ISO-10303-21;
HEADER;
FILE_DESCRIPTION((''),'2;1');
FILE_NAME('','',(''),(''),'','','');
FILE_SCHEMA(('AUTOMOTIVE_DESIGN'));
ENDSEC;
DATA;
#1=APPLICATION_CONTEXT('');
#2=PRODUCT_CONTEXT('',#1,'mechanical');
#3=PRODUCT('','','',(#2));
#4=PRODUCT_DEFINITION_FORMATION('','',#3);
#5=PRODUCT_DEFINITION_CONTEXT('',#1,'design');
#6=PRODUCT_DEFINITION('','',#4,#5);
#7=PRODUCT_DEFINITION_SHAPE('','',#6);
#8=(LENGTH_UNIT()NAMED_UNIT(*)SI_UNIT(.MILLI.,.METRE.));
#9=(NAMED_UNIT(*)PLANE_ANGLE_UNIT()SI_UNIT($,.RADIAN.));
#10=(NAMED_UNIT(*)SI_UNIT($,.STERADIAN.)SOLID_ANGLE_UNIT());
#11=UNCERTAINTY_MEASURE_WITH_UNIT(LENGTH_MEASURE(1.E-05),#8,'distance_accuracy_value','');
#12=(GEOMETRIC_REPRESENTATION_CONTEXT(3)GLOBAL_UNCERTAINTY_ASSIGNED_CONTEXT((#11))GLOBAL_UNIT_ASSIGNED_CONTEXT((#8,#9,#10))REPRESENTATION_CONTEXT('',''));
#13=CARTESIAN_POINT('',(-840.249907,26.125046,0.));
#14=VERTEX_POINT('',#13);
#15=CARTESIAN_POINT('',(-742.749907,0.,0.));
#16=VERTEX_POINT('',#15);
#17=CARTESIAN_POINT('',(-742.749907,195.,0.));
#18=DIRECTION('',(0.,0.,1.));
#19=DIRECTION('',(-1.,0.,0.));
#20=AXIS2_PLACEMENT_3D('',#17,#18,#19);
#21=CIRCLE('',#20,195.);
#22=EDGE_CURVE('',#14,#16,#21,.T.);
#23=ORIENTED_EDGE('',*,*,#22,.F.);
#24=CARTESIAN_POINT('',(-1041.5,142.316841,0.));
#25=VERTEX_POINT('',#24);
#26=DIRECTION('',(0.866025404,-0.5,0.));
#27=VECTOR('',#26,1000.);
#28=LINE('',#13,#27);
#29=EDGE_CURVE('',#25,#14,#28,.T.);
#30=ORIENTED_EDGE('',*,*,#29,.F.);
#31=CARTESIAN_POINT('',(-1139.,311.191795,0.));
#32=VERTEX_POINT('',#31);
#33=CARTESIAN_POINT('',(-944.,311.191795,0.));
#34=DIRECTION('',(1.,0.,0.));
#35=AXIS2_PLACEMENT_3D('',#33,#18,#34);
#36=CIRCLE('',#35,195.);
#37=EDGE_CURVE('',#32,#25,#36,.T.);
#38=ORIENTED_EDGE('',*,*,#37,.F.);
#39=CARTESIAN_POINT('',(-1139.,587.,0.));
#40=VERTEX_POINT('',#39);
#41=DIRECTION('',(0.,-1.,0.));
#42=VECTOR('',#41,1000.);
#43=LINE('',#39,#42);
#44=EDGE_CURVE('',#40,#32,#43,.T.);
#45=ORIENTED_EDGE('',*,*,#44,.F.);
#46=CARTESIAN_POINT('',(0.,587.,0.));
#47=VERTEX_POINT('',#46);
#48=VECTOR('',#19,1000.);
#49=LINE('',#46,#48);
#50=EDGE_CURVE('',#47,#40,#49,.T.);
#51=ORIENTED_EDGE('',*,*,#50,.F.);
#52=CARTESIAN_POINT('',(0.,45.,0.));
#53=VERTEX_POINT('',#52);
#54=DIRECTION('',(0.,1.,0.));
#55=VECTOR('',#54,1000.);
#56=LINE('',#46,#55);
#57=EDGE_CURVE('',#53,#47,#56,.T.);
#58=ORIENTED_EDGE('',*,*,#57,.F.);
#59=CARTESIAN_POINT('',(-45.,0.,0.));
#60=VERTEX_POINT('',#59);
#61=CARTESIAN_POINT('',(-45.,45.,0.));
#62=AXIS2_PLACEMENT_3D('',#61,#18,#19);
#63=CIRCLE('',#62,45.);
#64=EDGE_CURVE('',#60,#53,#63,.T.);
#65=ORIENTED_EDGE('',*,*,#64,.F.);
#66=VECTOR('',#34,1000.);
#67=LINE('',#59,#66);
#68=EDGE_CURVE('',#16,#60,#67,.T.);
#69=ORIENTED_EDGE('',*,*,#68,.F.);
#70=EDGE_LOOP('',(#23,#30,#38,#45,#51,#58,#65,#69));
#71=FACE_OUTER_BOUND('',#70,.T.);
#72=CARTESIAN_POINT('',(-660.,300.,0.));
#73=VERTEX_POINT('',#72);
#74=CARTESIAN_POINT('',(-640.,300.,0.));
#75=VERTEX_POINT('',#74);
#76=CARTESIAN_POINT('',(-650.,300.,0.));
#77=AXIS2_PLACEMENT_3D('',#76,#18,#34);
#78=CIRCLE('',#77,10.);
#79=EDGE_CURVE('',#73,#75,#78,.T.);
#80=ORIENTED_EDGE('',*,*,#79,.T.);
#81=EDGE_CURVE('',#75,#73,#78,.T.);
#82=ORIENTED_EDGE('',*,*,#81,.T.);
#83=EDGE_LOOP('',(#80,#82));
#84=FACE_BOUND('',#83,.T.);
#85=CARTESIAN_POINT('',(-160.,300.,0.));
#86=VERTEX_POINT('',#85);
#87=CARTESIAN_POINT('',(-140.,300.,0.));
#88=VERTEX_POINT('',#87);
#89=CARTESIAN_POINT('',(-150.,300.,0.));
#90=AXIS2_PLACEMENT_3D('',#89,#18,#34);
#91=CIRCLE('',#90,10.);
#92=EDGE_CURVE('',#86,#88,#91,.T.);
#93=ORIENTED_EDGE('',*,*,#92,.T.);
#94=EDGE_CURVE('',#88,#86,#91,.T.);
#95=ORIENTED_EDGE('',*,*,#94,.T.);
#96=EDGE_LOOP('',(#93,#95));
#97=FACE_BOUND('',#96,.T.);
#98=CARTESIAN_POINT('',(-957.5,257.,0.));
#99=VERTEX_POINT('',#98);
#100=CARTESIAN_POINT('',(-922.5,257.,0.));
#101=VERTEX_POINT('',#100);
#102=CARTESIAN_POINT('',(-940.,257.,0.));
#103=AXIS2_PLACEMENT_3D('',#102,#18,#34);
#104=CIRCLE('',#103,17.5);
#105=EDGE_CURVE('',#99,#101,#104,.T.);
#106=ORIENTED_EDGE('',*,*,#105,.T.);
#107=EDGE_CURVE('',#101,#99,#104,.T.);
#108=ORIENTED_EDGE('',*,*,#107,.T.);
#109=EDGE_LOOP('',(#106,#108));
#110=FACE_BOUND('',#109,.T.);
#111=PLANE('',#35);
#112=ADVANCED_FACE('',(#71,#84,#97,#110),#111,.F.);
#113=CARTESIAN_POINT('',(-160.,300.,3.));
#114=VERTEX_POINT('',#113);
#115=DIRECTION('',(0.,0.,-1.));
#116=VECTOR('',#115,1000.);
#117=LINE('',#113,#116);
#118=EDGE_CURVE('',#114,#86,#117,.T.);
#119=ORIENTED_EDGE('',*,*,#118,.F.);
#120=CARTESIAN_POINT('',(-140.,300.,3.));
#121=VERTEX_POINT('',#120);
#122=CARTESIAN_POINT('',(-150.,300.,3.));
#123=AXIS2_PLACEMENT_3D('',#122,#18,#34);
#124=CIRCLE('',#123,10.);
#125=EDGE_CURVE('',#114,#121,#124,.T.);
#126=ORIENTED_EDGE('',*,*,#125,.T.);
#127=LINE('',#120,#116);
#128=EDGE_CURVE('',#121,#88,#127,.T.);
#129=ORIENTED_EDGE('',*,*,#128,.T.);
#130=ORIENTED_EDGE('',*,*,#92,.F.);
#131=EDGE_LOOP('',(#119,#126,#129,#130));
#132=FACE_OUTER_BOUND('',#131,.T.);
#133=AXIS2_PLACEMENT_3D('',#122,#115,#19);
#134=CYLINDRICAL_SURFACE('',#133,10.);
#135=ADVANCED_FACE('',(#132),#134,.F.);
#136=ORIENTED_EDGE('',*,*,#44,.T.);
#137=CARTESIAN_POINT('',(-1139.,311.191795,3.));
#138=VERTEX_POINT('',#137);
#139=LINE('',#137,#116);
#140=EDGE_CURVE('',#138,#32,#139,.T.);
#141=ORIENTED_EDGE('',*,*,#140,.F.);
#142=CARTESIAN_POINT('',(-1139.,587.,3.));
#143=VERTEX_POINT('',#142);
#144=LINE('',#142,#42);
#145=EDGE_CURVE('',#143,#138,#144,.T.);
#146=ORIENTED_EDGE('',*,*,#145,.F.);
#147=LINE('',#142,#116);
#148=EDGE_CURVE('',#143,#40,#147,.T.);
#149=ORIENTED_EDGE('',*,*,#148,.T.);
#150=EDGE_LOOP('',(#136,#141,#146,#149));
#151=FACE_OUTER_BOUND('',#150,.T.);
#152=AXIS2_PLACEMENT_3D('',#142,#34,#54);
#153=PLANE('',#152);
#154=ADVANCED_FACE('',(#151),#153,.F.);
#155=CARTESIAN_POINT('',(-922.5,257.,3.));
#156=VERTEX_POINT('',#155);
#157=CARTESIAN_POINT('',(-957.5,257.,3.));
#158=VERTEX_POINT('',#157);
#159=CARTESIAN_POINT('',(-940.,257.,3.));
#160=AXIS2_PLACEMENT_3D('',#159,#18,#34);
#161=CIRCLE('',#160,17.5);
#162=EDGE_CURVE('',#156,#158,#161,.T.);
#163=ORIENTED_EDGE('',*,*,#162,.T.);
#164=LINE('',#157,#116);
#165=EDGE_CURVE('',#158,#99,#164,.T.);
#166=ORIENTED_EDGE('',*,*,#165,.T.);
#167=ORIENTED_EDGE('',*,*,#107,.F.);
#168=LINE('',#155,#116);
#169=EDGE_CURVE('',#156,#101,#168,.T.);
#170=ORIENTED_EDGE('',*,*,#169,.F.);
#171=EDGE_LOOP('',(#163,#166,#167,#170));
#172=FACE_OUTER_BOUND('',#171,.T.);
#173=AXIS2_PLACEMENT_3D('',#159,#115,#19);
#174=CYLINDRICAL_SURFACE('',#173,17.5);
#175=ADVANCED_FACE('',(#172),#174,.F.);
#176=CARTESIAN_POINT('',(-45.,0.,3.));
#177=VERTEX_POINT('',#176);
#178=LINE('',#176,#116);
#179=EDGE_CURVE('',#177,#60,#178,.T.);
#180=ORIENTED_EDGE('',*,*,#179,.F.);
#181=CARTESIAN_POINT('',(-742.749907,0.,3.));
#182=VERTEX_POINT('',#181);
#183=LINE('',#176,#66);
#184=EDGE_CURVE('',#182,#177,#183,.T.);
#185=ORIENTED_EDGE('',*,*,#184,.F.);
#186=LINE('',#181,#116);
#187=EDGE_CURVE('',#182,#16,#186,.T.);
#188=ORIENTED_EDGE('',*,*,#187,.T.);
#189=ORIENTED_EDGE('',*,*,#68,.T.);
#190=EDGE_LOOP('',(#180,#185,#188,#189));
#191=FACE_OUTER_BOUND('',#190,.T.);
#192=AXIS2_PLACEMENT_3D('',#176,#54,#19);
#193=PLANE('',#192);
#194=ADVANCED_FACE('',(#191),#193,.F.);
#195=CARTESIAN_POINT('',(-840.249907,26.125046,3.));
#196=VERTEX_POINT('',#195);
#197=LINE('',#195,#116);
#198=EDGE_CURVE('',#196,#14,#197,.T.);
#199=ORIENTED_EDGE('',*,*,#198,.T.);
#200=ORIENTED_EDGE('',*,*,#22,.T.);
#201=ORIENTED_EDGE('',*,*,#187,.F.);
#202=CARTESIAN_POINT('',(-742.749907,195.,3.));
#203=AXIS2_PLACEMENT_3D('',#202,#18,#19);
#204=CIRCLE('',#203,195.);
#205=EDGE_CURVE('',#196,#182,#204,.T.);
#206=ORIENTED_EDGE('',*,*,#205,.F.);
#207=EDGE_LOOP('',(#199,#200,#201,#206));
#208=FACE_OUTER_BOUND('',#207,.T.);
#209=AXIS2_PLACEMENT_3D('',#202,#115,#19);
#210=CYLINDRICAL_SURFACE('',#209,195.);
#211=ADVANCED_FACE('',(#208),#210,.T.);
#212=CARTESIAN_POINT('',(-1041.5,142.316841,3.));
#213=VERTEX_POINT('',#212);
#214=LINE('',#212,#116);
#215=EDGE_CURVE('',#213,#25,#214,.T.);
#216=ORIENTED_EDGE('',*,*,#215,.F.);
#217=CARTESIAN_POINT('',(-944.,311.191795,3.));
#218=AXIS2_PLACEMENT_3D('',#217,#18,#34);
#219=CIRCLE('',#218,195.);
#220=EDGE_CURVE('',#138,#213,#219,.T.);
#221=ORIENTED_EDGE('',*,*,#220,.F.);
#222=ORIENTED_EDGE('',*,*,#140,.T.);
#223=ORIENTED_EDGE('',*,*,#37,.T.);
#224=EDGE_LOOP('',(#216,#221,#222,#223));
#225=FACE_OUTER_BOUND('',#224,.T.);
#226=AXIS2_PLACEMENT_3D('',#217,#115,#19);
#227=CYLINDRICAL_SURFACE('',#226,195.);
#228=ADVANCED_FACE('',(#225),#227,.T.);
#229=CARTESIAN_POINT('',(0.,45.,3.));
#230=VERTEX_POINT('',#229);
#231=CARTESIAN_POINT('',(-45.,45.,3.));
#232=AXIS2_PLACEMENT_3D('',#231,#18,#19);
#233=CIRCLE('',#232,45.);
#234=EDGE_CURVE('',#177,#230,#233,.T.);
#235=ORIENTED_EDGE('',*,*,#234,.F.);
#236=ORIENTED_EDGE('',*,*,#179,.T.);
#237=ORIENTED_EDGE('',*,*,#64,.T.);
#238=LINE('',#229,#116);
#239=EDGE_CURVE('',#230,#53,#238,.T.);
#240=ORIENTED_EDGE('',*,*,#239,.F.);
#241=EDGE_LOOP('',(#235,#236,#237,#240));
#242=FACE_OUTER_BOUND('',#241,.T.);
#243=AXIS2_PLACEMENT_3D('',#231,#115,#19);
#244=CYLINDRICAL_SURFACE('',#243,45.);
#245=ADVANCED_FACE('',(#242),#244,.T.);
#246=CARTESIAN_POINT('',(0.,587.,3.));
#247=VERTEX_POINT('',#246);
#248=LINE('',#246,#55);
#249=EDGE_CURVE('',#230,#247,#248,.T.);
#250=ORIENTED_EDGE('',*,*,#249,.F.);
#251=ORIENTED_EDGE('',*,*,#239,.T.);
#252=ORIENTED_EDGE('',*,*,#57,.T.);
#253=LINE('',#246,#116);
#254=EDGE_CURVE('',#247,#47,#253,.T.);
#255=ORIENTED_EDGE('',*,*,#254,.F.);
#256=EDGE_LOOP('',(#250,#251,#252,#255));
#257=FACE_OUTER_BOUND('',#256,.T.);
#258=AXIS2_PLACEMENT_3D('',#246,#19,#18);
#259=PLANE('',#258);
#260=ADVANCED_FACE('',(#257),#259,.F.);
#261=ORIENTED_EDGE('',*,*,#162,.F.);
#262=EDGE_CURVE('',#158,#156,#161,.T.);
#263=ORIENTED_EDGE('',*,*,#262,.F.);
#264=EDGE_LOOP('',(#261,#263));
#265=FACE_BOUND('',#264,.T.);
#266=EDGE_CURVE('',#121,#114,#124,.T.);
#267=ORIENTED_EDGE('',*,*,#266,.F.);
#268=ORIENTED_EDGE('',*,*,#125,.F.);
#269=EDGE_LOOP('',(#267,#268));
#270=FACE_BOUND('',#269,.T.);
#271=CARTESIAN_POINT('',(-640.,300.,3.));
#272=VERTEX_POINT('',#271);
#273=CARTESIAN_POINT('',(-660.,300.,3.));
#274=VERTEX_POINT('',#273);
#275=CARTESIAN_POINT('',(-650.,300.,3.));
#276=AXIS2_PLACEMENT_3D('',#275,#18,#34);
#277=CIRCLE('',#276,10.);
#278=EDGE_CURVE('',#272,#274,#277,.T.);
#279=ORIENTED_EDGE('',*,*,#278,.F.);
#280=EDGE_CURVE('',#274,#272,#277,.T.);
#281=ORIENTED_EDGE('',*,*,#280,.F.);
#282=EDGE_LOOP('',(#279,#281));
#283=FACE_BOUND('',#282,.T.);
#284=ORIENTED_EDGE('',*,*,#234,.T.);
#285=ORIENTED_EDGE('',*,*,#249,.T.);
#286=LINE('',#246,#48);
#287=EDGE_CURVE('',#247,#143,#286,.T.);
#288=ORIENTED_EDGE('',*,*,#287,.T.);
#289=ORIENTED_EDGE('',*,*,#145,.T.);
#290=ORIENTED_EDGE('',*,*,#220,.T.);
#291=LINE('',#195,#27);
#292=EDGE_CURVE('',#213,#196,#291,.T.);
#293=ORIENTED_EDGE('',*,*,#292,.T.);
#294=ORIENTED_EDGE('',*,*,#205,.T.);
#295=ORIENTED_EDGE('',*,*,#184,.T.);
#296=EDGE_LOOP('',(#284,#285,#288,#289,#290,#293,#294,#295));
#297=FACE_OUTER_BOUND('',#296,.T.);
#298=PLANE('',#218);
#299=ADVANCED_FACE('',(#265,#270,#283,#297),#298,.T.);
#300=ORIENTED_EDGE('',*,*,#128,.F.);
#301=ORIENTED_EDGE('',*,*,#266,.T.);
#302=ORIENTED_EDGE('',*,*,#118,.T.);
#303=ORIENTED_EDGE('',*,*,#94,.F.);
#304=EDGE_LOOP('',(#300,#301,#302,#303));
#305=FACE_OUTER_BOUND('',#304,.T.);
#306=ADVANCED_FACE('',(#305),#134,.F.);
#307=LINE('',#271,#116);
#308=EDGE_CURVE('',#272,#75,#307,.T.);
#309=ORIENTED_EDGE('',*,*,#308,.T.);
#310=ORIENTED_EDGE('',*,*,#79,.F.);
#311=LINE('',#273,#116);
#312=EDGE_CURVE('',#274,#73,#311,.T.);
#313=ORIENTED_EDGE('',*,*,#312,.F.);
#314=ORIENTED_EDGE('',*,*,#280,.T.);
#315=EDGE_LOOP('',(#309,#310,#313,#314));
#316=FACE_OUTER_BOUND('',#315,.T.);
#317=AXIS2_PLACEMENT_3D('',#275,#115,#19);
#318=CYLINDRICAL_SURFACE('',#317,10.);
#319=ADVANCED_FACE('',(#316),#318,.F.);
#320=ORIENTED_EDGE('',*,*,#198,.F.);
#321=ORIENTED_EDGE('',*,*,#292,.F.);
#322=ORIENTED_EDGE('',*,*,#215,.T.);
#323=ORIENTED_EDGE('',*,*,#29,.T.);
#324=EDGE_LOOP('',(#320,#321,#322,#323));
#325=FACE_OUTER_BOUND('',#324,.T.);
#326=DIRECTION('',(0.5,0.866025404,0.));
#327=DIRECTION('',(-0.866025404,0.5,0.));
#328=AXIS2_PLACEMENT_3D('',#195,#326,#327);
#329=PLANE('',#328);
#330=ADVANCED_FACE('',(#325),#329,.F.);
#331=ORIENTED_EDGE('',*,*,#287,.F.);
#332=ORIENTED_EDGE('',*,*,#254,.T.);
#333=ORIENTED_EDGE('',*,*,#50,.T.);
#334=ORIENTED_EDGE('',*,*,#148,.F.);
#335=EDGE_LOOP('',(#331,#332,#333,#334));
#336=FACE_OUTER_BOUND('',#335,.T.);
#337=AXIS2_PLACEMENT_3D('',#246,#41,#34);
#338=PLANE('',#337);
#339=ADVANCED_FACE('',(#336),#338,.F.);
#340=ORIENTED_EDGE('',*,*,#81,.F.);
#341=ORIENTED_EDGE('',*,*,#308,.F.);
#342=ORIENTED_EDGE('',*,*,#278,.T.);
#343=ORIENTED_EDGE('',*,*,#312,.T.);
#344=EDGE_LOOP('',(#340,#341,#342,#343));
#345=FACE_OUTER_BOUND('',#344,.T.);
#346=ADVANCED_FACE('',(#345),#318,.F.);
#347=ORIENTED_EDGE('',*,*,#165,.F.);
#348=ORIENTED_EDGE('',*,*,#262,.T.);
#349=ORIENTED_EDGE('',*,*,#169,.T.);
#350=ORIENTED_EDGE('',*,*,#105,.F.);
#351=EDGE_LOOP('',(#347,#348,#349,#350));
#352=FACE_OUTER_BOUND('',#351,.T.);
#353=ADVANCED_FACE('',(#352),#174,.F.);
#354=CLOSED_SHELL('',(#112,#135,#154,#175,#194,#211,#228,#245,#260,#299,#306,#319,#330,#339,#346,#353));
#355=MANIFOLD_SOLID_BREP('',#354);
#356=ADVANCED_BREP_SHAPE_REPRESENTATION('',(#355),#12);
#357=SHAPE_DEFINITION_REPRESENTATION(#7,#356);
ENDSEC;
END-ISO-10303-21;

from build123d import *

# Parameters (mm, degrees)
SKETCH1_R           = 10
SKETCH1_R_2         = 17.5
BOSS_EXTRUDE1_DEPTH = 3


with BuildPart() as part:
    # Sketch1 → Boss-Extrude1 (new body)
    with BuildSketch(Plane.XY):
        with BuildLine():
            Line((0, 587), (0, 45))
            ThreePointArc((0, 45), (-13.180194847, 13.180194847), (-45, 0))
            Line((-45, 0), (-742.749907476, 0))
            ThreePointArc((-742.749907476, 0), (-793.219621271, 6.644463874), (-840.249907476, 26.125046262))
            Line((-840.249907476, 26.125046262), (-1041.5, 142.316841355))
            ThreePointArc((-1041.5, 142.316841355), (-1112.874953738, 213.691795093), (-1139, 311.191795093))
            Line((-1139, 311.191795093), (-1139, 587))
            Line((-1139, 587), (0, 587))
        make_face()
        with Locations((-650, 300)):
            Circle(SKETCH1_R, mode=Mode.SUBTRACT)
        with Locations((-150, 300)):
            Circle(SKETCH1_R, mode=Mode.SUBTRACT)
        with Locations((-940, 257)):
            Circle(SKETCH1_R_2, mode=Mode.SUBTRACT)
    extrude(amount=BOSS_EXTRUDE1_DEPTH)


solid = part.part
